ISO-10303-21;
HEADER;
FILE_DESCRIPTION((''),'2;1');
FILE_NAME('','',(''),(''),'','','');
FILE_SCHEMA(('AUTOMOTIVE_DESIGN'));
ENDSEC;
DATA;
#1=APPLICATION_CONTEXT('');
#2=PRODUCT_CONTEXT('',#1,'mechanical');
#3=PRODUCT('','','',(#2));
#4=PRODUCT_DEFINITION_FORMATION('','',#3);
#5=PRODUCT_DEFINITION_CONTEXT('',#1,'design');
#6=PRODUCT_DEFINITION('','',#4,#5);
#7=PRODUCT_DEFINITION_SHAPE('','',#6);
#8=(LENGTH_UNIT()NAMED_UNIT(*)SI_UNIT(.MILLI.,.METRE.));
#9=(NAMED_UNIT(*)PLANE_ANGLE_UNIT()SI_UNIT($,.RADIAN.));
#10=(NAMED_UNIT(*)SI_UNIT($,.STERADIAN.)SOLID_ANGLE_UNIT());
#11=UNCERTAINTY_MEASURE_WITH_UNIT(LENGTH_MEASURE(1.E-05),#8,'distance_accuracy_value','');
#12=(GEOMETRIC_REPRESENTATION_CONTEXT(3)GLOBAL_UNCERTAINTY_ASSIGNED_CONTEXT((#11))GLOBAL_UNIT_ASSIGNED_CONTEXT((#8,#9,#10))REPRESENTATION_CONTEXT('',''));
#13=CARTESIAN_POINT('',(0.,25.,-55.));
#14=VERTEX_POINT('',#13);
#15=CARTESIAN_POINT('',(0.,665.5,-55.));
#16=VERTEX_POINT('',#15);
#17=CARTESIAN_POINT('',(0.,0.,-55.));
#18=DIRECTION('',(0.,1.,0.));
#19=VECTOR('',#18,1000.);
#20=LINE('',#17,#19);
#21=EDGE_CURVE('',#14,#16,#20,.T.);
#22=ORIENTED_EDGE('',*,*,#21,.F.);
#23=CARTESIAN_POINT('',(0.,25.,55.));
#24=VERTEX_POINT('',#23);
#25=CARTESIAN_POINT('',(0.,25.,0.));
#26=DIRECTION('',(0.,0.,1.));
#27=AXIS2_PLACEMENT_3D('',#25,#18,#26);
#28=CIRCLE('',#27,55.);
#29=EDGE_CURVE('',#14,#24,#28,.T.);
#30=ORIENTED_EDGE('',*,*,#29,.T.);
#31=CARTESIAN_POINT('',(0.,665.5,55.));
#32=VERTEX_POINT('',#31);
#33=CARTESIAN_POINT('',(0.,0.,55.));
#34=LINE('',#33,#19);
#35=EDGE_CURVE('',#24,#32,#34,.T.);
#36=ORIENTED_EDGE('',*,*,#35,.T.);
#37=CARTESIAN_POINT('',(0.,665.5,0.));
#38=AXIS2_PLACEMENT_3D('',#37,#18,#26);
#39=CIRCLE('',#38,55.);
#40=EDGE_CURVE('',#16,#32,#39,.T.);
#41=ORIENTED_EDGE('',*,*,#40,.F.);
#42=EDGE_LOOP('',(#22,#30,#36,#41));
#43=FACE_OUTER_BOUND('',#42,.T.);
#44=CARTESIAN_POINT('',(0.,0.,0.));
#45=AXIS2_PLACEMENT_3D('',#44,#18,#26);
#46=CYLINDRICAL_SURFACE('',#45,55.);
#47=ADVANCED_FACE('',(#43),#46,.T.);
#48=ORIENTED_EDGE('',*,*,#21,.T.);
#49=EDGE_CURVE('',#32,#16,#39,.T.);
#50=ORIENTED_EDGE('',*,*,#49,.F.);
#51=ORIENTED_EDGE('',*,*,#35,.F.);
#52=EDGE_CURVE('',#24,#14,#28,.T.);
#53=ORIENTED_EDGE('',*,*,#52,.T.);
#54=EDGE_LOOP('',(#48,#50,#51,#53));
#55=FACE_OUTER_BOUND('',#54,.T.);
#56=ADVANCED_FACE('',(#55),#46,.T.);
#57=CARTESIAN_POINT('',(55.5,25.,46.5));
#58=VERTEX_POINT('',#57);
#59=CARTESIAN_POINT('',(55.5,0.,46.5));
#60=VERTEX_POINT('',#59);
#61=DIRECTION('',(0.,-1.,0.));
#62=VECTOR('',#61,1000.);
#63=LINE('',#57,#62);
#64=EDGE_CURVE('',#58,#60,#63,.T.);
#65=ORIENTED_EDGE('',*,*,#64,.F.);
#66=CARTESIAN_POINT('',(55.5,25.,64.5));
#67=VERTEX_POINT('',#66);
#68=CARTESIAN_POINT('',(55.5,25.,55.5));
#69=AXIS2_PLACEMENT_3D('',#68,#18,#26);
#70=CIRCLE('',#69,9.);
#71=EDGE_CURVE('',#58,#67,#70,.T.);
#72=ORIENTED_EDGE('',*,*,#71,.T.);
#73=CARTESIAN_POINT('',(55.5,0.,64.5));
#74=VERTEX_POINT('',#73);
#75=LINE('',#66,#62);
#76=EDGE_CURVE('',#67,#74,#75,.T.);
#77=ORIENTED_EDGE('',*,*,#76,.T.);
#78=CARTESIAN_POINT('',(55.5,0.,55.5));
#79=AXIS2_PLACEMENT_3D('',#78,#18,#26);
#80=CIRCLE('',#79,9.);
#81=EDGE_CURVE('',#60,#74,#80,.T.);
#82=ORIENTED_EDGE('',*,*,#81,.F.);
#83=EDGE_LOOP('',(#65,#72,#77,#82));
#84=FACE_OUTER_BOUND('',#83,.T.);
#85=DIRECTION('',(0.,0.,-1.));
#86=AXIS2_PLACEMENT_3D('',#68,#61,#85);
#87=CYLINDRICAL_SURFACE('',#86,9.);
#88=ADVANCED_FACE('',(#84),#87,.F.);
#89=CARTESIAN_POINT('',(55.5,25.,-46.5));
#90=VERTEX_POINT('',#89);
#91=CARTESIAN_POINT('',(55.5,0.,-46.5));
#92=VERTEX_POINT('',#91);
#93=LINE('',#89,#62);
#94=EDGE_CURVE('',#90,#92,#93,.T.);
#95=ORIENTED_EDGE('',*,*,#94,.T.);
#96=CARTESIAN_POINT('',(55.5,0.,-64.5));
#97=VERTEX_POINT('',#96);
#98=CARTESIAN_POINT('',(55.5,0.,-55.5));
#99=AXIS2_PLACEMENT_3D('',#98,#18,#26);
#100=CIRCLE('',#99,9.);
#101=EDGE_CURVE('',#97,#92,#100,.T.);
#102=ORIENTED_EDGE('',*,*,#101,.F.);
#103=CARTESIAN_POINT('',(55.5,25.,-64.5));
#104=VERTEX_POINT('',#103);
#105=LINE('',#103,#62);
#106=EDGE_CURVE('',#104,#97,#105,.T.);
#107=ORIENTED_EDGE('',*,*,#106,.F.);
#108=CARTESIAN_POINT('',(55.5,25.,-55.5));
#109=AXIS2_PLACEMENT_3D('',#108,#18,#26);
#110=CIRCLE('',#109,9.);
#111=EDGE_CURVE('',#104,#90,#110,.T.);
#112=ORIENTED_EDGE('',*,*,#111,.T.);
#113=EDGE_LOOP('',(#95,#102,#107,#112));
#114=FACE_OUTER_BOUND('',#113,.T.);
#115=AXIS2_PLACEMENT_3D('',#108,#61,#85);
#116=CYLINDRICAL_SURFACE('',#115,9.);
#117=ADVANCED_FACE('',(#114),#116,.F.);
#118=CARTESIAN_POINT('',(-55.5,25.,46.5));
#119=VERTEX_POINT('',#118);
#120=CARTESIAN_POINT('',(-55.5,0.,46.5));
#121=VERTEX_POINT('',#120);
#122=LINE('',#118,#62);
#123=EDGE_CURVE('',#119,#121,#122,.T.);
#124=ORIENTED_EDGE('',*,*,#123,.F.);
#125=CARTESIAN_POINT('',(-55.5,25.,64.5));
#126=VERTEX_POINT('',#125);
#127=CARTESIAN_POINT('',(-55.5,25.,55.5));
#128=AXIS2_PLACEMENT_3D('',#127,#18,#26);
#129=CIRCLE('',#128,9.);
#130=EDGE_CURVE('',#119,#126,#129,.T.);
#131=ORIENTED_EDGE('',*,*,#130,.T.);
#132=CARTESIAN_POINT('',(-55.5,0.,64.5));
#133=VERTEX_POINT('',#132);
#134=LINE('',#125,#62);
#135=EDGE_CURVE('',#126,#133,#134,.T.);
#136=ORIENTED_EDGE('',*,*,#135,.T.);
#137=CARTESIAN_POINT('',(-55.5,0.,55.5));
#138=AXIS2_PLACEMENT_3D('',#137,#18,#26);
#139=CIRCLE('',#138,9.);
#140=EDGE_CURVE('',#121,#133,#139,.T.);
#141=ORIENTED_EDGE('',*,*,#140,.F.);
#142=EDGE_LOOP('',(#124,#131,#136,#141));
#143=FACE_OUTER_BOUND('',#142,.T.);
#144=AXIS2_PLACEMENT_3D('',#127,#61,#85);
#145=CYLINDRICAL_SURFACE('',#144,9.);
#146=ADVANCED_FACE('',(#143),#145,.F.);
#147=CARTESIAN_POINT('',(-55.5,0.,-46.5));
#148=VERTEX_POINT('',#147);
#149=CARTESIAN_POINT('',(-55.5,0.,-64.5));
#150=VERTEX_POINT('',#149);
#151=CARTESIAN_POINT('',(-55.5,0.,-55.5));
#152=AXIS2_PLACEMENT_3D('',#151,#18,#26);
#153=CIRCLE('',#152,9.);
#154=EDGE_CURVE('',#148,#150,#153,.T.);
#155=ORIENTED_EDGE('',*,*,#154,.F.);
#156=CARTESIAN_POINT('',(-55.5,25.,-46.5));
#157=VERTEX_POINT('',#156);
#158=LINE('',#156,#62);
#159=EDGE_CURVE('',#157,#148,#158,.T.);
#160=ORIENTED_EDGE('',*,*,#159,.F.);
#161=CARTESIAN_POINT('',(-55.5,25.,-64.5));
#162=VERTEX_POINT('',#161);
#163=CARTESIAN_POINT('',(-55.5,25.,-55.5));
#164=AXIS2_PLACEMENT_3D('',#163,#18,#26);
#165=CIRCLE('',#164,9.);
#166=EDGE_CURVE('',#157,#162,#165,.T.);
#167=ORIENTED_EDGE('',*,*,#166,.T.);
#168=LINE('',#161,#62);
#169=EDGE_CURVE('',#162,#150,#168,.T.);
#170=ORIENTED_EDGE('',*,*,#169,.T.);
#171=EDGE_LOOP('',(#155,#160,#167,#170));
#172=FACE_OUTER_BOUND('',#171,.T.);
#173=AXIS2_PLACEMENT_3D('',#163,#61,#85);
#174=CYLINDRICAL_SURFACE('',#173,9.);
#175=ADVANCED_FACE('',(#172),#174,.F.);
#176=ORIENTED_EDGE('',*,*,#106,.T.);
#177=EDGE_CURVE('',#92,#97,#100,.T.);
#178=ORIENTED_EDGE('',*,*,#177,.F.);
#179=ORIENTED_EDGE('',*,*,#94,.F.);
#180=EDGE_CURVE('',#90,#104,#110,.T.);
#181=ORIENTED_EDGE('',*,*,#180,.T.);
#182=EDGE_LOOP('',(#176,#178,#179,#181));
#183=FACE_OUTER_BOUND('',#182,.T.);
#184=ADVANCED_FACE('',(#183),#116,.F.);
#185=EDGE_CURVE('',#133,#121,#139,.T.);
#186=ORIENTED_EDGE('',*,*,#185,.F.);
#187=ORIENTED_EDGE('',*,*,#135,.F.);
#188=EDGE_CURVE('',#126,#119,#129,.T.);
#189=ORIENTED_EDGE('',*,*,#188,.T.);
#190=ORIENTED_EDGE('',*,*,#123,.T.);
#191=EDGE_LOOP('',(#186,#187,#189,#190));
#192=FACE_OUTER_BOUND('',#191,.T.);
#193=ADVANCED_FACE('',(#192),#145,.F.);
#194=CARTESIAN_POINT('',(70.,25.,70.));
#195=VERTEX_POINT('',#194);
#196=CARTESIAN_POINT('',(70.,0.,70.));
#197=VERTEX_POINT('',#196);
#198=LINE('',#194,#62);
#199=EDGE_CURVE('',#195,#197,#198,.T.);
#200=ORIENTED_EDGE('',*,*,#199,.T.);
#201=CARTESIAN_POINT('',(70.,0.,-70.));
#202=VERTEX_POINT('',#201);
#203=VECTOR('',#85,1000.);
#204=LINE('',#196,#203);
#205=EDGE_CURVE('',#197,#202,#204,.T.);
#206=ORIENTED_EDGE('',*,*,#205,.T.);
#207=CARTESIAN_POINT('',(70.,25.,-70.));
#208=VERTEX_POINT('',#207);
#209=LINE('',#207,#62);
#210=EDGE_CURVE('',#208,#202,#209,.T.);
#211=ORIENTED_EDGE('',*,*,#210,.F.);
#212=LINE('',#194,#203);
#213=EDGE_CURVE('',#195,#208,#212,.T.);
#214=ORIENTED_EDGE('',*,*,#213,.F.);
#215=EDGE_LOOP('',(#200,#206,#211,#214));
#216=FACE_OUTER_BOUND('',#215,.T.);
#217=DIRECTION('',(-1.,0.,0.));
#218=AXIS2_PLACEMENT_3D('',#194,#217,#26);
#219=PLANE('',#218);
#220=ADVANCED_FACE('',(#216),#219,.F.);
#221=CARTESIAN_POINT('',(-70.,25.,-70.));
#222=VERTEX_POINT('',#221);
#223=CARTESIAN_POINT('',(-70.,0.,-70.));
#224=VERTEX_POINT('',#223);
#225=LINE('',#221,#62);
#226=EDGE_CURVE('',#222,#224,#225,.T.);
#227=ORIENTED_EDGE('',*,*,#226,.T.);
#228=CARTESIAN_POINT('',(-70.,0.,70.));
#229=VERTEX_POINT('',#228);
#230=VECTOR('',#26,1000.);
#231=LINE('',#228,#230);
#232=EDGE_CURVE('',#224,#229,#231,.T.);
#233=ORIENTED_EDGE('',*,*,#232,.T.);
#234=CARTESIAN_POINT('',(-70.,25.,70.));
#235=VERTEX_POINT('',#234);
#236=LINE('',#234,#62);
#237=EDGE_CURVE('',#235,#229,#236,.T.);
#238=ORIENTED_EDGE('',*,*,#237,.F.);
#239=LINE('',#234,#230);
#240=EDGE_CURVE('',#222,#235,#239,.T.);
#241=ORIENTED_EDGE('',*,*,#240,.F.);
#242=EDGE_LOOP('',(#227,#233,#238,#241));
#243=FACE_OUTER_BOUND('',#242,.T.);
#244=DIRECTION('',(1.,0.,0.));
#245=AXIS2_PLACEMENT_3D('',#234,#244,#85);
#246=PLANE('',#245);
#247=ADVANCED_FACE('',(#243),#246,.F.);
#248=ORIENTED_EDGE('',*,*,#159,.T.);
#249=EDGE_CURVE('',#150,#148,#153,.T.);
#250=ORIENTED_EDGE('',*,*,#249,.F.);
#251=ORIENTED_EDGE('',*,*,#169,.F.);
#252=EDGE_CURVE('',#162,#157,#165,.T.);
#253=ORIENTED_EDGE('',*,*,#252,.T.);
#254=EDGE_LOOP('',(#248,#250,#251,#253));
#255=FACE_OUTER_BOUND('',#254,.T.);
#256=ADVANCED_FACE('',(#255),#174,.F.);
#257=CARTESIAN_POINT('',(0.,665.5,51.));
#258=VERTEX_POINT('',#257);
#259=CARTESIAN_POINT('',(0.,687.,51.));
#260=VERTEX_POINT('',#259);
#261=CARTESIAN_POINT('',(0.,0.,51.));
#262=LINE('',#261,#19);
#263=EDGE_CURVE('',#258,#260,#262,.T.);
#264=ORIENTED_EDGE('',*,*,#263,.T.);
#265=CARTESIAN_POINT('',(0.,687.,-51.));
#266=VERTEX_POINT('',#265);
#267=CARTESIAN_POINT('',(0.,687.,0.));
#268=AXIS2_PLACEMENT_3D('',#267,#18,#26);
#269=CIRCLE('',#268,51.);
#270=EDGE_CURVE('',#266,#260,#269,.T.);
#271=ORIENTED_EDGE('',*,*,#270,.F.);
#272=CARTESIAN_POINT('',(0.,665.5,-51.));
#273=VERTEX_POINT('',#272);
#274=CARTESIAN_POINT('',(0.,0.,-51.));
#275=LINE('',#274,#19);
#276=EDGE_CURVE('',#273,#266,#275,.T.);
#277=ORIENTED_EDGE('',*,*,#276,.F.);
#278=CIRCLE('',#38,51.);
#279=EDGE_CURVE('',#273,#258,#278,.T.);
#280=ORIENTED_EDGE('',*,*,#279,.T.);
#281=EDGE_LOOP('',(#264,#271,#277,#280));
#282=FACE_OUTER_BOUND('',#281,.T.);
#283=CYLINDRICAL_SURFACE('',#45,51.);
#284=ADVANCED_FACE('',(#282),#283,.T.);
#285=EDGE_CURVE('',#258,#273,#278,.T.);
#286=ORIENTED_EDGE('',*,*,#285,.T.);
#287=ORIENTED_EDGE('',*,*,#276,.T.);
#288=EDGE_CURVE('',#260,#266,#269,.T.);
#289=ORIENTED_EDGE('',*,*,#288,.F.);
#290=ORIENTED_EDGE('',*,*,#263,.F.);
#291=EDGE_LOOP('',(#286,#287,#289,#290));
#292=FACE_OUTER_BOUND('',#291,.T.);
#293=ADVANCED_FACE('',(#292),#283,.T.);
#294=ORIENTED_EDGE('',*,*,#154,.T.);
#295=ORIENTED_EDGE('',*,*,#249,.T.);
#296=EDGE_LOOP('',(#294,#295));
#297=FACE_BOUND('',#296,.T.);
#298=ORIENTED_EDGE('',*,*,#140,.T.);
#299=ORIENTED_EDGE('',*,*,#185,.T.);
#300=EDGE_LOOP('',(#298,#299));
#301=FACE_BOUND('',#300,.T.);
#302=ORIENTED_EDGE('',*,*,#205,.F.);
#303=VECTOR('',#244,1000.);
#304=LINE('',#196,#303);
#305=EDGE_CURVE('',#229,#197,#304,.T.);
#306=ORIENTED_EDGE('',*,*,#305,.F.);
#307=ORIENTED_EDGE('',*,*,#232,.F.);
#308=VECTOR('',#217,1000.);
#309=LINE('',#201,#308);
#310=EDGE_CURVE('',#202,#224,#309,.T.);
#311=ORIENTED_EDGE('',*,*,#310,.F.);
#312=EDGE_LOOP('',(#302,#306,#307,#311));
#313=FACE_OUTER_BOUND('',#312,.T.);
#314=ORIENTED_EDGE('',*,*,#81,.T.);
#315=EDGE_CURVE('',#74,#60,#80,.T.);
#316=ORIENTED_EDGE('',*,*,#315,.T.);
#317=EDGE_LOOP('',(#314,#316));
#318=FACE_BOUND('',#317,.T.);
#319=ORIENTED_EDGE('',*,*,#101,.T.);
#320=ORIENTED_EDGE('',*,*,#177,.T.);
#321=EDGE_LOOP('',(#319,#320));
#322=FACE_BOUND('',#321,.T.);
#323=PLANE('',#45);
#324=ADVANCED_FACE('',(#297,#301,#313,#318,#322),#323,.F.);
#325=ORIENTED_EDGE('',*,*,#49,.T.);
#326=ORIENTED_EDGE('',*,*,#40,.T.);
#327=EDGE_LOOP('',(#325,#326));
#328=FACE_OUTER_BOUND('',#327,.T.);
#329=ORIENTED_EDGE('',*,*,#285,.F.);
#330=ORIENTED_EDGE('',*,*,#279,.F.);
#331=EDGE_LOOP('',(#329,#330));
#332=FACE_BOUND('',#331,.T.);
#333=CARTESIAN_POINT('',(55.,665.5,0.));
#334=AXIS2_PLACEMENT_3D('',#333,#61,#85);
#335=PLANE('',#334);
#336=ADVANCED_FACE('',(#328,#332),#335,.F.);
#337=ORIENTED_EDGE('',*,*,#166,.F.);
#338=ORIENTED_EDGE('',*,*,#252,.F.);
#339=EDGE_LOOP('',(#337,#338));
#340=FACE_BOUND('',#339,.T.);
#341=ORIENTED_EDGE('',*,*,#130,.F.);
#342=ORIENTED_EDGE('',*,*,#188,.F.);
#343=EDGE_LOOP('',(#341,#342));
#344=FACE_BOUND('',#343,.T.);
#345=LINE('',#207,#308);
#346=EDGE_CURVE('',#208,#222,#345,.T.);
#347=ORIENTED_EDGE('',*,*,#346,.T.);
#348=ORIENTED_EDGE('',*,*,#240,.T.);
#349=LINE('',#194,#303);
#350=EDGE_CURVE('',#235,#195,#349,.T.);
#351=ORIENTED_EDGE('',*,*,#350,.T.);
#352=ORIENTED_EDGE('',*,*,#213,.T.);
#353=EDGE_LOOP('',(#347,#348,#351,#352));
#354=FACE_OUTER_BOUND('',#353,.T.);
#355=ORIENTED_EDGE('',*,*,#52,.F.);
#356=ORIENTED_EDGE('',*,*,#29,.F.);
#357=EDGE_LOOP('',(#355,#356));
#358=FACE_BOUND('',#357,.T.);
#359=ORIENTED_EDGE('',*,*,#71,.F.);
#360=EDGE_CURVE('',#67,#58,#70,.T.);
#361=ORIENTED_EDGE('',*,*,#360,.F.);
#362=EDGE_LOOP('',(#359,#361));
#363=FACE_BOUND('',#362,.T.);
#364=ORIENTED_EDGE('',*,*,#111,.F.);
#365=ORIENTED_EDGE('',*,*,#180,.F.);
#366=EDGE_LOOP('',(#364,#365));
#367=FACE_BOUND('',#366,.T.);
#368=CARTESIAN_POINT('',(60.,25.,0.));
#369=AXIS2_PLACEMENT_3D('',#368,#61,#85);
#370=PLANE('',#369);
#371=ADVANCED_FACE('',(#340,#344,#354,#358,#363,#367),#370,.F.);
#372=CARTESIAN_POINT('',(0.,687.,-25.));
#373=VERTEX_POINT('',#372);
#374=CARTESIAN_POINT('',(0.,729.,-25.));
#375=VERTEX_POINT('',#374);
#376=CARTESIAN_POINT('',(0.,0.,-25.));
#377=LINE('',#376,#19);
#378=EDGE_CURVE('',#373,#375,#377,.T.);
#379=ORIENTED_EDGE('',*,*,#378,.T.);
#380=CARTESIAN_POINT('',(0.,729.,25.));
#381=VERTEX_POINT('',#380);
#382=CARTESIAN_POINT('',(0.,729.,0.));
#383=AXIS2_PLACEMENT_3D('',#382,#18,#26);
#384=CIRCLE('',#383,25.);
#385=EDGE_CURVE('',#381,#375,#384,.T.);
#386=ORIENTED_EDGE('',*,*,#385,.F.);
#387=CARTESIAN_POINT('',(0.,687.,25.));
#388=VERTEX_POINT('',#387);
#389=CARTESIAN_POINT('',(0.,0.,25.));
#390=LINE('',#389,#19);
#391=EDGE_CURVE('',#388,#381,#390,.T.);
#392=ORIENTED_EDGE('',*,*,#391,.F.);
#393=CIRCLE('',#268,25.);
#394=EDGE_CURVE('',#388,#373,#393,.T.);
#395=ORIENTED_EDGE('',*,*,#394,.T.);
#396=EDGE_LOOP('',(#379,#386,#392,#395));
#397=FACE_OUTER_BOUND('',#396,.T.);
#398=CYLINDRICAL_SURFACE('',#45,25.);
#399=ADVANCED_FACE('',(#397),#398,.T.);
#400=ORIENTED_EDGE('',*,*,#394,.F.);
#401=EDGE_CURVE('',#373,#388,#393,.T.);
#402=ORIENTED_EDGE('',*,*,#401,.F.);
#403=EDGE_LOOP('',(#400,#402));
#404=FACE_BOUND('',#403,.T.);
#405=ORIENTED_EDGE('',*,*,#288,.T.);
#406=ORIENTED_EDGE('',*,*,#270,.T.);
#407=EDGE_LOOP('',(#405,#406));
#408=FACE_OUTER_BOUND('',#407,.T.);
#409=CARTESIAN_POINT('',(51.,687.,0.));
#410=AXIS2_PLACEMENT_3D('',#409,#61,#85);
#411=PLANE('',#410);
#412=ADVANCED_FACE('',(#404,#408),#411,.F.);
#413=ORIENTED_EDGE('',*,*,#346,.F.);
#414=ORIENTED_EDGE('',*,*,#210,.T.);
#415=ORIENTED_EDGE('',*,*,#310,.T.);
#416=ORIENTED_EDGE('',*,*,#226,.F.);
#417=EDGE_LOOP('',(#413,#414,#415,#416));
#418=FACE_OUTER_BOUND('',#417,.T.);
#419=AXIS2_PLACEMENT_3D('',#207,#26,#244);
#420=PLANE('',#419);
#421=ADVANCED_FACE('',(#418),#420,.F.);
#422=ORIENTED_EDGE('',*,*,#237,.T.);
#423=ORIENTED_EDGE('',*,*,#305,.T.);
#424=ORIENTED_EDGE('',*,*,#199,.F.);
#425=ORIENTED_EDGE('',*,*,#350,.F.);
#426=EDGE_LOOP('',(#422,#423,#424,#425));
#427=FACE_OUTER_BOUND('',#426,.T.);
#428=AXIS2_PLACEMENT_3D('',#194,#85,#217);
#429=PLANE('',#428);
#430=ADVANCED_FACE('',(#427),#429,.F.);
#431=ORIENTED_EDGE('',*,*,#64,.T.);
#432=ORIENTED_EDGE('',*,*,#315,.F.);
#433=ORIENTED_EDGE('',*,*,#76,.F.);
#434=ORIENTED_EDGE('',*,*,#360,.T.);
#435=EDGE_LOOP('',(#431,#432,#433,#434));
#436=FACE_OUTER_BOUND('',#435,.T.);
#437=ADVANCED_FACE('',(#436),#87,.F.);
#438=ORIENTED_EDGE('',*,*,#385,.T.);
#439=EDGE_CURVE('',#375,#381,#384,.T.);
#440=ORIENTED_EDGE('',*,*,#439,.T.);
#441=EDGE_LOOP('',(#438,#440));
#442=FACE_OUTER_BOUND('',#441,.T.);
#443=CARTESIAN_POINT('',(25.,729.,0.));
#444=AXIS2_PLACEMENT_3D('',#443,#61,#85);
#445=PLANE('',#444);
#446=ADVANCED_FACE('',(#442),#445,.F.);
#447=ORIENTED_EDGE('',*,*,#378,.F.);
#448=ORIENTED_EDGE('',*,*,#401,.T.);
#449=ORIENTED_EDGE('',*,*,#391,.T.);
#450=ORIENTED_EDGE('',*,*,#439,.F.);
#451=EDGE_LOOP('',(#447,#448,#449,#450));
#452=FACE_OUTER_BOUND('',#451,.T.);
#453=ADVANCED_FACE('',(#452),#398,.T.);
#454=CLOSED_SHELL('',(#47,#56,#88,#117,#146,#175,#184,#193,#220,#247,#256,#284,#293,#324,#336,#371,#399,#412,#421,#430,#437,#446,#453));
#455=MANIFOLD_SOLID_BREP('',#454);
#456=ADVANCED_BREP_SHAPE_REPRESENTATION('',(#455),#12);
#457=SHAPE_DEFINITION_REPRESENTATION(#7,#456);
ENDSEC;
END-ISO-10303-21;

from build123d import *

# Parameters (mm, degrees)
SKETCH2_W           = 140
SKETCH2_H           = 140
SKETCH2_R           = 9
BOSS_EXTRUDE1_DEPTH = 25


with BuildPart() as part:
    # Sketch1 → Revolve1 (revolve)
    with BuildSketch(Plane.XY, mode=Mode.PRIVATE) as revolve1_sk:
        Polygon((0, 0), (60, 0), (60, 25), (55, 25), (55, 665.5), (51, 665.5), (51, 687), (25, 687), (25, 729), (0, 729), align=None)
    revolve(revolve1_sk.sketch.rotate(Axis((0, 0, 0), (0, -1, 0)), 90), axis=Axis((0, 0, 0), (0, -1, 0)))

    # Sketch2 → Boss-Extrude1 (add)
    with BuildSketch(Plane(origin=(0, 0, 0), x_dir=(1, 0, 0), z_dir=(0, 1, 0))):
        Rectangle(SKETCH2_W, SKETCH2_H)
        with Locations(Location((-55.5, 55.5, 0), (0, 0, 270))):
            Circle(SKETCH2_R, mode=Mode.SUBTRACT)
        with Locations(Location((55.5, 55.5, 0), (0, 0, 270))):
            Circle(SKETCH2_R, mode=Mode.SUBTRACT)
        with Locations(Location((55.5, -55.5, 0), (0, 0, 270))):
            Circle(SKETCH2_R, mode=Mode.SUBTRACT)
        with Locations(Location((-55.5, -55.5, 0), (0, 0, 270))):
            Circle(SKETCH2_R, mode=Mode.SUBTRACT)
    extrude(amount=BOSS_EXTRUDE1_DEPTH)


solid = part.part
